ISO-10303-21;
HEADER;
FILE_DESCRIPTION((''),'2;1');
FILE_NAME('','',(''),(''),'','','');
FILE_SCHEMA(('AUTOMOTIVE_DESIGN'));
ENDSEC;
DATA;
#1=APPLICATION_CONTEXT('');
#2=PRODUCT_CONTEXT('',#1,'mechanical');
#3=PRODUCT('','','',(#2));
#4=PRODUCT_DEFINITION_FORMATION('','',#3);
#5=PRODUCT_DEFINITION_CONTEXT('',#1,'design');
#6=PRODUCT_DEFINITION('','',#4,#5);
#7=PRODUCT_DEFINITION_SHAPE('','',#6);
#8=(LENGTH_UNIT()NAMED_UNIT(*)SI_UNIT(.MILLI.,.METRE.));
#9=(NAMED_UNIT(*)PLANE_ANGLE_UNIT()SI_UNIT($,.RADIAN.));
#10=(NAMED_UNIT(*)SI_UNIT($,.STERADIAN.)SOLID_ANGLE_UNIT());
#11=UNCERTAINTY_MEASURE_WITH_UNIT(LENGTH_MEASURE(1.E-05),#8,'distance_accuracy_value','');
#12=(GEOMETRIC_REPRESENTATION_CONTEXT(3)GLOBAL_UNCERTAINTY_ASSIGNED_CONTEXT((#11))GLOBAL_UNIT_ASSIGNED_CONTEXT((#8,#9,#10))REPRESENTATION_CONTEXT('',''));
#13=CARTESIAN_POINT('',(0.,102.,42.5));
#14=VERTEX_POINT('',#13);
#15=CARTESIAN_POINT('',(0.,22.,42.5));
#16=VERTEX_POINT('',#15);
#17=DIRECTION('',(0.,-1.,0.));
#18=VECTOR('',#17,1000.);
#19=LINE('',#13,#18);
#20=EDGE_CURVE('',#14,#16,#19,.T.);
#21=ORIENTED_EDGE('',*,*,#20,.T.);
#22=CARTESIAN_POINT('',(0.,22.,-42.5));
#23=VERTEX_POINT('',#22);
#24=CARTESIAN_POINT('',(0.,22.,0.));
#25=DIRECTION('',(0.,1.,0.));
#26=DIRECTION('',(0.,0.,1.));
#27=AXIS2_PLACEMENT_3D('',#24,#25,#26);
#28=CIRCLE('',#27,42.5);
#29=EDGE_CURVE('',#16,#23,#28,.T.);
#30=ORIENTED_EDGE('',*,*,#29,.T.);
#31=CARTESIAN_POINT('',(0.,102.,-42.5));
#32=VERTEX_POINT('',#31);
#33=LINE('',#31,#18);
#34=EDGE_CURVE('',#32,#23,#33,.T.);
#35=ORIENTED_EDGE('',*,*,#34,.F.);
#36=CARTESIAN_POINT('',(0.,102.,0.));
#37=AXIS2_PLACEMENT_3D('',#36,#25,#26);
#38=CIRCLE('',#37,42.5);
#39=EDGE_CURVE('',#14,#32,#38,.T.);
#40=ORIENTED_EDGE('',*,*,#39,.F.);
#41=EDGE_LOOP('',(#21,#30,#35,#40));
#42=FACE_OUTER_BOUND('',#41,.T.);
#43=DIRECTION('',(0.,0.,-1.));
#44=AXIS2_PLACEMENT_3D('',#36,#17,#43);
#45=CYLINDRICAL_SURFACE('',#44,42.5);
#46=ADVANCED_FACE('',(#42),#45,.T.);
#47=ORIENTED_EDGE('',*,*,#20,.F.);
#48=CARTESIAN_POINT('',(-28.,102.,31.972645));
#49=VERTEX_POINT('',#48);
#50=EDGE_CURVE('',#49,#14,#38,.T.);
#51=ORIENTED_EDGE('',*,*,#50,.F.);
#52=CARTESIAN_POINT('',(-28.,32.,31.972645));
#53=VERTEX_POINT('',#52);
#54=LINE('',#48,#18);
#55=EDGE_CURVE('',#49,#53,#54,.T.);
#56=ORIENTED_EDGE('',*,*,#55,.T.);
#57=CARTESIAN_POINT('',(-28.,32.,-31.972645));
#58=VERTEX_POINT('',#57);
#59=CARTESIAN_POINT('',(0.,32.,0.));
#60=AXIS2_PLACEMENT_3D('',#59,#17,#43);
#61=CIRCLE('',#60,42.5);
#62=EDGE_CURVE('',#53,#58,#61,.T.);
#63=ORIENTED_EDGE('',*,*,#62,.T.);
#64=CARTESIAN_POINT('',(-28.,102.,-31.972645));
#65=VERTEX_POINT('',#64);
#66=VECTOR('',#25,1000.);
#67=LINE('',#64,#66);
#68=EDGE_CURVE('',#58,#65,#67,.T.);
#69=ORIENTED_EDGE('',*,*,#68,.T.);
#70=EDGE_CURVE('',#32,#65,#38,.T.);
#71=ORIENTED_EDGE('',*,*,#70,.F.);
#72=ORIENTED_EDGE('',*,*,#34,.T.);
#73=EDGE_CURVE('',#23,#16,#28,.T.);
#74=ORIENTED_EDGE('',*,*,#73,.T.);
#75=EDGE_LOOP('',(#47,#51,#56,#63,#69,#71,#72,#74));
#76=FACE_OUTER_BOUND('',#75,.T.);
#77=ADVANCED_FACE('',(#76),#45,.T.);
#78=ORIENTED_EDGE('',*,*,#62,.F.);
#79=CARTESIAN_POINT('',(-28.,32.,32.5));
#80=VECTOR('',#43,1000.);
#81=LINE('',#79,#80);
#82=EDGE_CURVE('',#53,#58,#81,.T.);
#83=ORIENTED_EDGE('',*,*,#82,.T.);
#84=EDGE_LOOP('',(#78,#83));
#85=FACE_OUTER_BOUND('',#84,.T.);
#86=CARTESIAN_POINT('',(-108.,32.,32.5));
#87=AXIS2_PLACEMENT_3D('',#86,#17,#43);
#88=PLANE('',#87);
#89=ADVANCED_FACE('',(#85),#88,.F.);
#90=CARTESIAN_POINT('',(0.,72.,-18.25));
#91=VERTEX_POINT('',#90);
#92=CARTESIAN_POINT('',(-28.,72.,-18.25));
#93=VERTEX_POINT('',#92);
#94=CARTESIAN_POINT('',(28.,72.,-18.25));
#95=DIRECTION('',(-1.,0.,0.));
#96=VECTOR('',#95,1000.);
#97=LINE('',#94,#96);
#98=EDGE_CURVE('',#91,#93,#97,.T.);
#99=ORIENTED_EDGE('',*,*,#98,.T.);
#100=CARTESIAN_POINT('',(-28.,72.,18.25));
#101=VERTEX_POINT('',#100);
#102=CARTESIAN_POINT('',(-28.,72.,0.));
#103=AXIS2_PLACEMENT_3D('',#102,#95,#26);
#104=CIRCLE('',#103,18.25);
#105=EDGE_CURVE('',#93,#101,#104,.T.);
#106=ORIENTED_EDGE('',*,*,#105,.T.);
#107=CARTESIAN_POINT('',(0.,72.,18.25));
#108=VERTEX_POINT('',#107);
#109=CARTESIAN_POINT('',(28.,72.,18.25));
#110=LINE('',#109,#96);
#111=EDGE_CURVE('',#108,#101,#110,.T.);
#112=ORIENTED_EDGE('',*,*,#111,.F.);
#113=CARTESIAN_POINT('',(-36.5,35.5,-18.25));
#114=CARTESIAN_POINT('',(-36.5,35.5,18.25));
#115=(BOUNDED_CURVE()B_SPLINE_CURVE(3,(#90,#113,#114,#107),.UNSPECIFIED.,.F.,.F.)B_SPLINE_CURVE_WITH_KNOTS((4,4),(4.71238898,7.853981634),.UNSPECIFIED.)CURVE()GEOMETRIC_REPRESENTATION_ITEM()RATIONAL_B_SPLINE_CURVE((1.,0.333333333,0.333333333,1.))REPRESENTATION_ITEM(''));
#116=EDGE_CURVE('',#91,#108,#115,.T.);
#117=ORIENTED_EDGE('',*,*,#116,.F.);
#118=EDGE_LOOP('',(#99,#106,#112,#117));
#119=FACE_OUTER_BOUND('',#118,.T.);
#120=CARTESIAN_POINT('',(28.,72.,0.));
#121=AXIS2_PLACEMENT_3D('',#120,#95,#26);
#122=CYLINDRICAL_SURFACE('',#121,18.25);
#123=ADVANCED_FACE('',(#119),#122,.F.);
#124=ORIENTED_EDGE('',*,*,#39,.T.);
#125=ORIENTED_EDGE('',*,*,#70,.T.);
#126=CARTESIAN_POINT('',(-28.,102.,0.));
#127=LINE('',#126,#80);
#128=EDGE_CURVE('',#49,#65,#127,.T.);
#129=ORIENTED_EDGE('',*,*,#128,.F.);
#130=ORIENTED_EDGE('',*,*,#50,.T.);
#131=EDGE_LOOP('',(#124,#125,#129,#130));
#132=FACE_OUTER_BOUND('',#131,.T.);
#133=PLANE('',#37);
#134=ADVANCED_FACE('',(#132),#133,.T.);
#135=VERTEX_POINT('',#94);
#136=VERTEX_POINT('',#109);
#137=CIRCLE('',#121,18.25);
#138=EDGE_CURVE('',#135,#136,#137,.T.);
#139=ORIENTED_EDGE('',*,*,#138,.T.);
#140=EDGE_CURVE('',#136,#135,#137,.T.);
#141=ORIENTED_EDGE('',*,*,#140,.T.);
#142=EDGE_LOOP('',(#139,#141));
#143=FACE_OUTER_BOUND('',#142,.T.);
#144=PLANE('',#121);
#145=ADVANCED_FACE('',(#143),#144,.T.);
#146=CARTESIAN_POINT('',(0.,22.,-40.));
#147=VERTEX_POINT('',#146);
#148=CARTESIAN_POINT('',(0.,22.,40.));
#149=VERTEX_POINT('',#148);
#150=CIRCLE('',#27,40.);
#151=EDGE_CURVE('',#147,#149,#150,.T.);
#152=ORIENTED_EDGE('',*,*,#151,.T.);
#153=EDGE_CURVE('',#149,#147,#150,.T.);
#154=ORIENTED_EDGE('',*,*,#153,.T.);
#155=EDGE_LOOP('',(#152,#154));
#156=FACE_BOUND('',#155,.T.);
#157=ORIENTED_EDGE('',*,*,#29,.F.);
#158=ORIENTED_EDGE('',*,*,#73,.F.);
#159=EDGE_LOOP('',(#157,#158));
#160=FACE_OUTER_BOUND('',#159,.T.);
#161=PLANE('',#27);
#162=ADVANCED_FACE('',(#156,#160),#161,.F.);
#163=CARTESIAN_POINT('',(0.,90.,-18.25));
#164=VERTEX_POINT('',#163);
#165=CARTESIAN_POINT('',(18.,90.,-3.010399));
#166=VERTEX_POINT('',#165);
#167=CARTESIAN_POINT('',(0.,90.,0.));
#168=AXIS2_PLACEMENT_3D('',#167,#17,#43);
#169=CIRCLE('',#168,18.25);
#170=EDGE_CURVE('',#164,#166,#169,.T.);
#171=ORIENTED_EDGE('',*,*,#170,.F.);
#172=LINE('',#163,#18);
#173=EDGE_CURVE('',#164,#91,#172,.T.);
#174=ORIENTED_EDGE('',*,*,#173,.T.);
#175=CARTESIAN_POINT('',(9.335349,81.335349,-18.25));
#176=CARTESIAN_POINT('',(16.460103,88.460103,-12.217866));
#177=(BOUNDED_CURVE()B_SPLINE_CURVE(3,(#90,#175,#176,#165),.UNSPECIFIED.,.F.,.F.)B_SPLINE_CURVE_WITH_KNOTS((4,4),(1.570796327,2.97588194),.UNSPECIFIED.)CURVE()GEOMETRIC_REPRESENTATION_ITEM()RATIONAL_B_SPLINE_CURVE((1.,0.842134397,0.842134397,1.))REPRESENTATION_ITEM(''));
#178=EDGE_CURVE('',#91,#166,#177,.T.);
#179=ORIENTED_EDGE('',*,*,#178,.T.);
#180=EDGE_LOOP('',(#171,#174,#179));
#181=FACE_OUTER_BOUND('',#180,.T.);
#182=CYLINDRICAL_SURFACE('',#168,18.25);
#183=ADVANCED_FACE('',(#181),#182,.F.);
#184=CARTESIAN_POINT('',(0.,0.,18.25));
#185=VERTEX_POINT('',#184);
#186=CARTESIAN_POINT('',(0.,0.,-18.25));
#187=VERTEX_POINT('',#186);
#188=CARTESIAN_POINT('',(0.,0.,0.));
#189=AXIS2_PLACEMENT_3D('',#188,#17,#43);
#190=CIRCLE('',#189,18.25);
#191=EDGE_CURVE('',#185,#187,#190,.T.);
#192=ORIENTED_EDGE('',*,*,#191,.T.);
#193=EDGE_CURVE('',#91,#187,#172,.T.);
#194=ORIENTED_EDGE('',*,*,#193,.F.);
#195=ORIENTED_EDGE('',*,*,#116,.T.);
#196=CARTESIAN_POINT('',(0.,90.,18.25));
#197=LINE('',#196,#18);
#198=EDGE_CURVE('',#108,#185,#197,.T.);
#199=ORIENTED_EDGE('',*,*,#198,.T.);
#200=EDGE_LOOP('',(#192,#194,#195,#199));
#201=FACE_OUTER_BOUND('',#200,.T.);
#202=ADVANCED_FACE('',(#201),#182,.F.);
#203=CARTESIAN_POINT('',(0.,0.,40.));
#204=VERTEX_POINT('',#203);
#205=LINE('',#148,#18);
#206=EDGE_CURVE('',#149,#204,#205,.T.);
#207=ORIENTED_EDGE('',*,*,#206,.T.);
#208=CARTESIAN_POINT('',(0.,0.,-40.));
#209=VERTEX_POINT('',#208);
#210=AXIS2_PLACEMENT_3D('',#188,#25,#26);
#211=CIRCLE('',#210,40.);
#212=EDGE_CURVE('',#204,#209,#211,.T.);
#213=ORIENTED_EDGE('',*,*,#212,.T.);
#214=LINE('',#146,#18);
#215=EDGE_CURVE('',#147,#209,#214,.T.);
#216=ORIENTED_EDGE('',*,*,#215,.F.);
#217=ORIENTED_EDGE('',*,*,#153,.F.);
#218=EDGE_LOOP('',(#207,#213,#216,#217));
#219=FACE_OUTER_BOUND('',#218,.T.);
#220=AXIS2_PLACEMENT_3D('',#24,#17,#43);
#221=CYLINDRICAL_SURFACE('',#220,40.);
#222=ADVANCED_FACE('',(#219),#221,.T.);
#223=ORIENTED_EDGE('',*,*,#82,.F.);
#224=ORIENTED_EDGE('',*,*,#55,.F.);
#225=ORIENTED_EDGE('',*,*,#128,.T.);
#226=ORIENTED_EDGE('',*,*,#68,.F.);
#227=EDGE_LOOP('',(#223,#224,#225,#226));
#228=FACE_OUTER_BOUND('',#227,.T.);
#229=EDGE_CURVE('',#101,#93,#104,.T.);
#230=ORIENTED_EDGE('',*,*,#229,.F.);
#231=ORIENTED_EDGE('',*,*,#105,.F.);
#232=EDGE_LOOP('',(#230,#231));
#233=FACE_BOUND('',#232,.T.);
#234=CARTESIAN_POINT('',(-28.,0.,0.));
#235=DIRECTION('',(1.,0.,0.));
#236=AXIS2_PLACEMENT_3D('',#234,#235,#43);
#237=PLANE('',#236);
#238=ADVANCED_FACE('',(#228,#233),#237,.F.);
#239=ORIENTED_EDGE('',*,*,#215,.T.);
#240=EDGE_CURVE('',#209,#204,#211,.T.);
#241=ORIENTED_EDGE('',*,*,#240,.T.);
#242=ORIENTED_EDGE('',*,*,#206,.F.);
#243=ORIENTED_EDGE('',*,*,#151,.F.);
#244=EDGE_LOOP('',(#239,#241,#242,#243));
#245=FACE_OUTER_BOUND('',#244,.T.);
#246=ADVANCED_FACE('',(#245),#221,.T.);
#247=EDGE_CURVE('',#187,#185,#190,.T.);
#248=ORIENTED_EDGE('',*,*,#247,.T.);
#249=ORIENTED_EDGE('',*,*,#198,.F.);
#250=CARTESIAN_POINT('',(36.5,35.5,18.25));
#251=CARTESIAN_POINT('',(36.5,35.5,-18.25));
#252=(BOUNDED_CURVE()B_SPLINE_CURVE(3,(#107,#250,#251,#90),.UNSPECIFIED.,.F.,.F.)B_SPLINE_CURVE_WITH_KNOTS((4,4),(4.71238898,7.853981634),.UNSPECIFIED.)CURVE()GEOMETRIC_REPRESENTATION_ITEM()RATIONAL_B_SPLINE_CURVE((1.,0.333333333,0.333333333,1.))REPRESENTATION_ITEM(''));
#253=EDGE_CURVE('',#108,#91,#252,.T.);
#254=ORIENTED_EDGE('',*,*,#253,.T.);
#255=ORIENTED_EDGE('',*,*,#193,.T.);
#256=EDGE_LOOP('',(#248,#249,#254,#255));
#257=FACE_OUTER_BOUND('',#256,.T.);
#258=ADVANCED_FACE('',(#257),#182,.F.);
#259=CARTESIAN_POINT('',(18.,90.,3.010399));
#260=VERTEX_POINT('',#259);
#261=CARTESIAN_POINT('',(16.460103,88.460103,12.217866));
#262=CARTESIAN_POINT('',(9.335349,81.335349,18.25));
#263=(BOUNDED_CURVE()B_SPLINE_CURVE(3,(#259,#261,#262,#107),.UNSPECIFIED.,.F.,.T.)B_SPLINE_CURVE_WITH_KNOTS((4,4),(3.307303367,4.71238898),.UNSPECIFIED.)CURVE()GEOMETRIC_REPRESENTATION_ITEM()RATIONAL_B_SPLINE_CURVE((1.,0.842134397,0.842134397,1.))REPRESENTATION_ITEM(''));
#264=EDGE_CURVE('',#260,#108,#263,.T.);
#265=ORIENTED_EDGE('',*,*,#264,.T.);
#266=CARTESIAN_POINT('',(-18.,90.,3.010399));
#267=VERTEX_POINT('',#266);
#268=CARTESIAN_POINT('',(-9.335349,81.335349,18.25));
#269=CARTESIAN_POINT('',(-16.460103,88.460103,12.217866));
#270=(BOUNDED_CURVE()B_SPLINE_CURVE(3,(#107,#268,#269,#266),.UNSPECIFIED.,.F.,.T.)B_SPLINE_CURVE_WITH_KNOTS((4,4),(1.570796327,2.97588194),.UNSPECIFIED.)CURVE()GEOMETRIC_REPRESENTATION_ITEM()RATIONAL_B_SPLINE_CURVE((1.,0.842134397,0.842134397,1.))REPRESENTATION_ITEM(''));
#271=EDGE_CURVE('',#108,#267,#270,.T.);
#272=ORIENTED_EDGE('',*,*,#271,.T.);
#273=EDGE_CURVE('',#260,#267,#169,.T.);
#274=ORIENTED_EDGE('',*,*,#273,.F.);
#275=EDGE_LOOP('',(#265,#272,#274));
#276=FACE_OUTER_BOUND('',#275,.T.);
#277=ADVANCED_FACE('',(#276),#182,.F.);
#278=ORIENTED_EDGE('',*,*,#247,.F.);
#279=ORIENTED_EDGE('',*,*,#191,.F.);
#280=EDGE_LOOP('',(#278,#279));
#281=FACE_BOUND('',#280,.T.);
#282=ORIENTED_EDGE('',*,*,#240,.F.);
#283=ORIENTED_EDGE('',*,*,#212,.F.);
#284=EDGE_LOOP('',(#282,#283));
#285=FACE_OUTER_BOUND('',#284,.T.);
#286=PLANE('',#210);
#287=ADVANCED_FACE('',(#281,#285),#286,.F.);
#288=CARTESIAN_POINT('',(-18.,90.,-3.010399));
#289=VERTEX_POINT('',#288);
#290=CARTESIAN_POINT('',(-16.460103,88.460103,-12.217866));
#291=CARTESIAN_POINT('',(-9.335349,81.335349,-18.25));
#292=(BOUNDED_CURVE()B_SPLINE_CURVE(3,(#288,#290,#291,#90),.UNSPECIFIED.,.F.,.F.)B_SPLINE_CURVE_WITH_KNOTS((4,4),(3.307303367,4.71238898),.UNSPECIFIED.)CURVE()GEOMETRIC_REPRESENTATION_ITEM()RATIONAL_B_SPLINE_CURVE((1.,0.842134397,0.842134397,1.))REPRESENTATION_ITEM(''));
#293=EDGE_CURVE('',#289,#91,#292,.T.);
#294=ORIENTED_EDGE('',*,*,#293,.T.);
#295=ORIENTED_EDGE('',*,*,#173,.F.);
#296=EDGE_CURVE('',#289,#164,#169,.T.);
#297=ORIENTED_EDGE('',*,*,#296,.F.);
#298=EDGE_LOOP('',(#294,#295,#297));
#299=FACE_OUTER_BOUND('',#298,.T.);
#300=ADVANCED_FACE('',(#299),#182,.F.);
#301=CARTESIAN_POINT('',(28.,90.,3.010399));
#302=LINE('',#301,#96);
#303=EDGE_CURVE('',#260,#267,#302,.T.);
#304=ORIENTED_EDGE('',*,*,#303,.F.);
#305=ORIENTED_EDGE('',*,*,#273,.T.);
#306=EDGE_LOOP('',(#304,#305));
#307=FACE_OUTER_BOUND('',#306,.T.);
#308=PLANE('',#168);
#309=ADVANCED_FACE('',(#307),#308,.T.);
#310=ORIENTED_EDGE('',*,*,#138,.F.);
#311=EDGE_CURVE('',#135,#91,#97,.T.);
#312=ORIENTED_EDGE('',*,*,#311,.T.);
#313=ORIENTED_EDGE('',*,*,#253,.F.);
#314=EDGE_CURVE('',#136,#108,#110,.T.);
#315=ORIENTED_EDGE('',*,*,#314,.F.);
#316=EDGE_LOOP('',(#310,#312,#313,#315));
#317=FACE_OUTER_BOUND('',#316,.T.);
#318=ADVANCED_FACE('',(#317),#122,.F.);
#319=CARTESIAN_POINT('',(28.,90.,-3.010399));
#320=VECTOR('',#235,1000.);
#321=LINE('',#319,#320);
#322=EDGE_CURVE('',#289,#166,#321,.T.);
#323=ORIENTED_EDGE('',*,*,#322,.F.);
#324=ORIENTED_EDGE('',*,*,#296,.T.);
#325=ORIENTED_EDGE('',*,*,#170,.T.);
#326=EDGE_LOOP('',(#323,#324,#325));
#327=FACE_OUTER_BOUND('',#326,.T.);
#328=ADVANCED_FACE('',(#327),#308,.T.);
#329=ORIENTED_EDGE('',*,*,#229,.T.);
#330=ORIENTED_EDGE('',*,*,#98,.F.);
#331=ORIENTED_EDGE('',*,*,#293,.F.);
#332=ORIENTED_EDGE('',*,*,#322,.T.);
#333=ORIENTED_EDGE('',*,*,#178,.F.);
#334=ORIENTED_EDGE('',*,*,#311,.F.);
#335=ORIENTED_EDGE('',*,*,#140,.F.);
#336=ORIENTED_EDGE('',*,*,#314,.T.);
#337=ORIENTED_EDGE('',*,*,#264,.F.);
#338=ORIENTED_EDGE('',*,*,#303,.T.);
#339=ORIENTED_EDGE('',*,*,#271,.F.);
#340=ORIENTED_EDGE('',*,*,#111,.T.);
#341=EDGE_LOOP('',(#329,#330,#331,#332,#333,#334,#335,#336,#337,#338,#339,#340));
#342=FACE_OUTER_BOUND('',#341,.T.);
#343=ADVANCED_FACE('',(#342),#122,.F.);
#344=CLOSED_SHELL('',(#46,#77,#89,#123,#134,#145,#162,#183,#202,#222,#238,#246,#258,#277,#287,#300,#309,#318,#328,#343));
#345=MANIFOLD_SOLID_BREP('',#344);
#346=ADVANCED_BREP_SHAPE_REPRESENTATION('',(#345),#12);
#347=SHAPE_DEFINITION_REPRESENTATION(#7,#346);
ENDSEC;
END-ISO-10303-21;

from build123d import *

# Parameters (mm, degrees)
SKETCH1_R           = 40
BOSS_EXTRUDE1_DEPTH = 22
SKETCH2_R           = 42.5
BOSS_EXTRUDE2_DEPTH = 80
CUT_EXTRUDE1_START  = -28
SKETCH3_W           = 65
SKETCH3_H           = 70
CUT_EXTRUDE1_DEPTH  = 80
SKETCH4_R           = 18.25
CUT_EXTRUDE2_DEPTH  = 90
SKETCH5_R           = 18.25
CUT_EXTRUDE3_DEPTH  = 56


with BuildPart() as part:
    # Sketch1 → Boss-Extrude1 (new body)
    with BuildSketch(Plane(origin=(0, 0, 0), x_dir=(1, 0, 0), z_dir=(0, 1, 0))):
        with Locations(Location((0, 0, 0), (0, 0, 270))):
            Circle(SKETCH1_R)
    extrude(amount=BOSS_EXTRUDE1_DEPTH)

    # Sketch2 → Boss-Extrude2 (add)
    with BuildSketch(Plane(origin=(0, 22, 0), x_dir=(1, 0, 0), z_dir=(0, 1, 0))):
        with Locations(Location((0, 0, 0), (0, 0, 270))):
            Circle(SKETCH2_R)
    extrude(amount=BOSS_EXTRUDE2_DEPTH)

    # Sketch3 → Cut-Extrude1 (cut)
    with BuildSketch(Plane(origin=(0, 0, 0), x_dir=(0, 0, -1), z_dir=(1, 0, 0)).offset(CUT_EXTRUDE1_START)):
        with Locations((0, 67)):
            Rectangle(SKETCH3_W, SKETCH3_H)
    extrude(amount=-CUT_EXTRUDE1_DEPTH, mode=Mode.SUBTRACT)

    # Sketch4 → Cut-Extrude2 (cut)
    with BuildSketch(Plane.XZ):
        with Locations(Location((0, 0, 0), (0, 0, 270))):
            Circle(SKETCH4_R)
    extrude(amount=-CUT_EXTRUDE2_DEPTH, mode=Mode.SUBTRACT)

    # Sketch5 → Cut-Extrude3 (cut)
    with BuildSketch(Plane.ZY.offset(28)):
        with Locations((0, 72)):
            Circle(SKETCH5_R)
    extrude(amount=-CUT_EXTRUDE3_DEPTH, mode=Mode.SUBTRACT)


solid = part.part
